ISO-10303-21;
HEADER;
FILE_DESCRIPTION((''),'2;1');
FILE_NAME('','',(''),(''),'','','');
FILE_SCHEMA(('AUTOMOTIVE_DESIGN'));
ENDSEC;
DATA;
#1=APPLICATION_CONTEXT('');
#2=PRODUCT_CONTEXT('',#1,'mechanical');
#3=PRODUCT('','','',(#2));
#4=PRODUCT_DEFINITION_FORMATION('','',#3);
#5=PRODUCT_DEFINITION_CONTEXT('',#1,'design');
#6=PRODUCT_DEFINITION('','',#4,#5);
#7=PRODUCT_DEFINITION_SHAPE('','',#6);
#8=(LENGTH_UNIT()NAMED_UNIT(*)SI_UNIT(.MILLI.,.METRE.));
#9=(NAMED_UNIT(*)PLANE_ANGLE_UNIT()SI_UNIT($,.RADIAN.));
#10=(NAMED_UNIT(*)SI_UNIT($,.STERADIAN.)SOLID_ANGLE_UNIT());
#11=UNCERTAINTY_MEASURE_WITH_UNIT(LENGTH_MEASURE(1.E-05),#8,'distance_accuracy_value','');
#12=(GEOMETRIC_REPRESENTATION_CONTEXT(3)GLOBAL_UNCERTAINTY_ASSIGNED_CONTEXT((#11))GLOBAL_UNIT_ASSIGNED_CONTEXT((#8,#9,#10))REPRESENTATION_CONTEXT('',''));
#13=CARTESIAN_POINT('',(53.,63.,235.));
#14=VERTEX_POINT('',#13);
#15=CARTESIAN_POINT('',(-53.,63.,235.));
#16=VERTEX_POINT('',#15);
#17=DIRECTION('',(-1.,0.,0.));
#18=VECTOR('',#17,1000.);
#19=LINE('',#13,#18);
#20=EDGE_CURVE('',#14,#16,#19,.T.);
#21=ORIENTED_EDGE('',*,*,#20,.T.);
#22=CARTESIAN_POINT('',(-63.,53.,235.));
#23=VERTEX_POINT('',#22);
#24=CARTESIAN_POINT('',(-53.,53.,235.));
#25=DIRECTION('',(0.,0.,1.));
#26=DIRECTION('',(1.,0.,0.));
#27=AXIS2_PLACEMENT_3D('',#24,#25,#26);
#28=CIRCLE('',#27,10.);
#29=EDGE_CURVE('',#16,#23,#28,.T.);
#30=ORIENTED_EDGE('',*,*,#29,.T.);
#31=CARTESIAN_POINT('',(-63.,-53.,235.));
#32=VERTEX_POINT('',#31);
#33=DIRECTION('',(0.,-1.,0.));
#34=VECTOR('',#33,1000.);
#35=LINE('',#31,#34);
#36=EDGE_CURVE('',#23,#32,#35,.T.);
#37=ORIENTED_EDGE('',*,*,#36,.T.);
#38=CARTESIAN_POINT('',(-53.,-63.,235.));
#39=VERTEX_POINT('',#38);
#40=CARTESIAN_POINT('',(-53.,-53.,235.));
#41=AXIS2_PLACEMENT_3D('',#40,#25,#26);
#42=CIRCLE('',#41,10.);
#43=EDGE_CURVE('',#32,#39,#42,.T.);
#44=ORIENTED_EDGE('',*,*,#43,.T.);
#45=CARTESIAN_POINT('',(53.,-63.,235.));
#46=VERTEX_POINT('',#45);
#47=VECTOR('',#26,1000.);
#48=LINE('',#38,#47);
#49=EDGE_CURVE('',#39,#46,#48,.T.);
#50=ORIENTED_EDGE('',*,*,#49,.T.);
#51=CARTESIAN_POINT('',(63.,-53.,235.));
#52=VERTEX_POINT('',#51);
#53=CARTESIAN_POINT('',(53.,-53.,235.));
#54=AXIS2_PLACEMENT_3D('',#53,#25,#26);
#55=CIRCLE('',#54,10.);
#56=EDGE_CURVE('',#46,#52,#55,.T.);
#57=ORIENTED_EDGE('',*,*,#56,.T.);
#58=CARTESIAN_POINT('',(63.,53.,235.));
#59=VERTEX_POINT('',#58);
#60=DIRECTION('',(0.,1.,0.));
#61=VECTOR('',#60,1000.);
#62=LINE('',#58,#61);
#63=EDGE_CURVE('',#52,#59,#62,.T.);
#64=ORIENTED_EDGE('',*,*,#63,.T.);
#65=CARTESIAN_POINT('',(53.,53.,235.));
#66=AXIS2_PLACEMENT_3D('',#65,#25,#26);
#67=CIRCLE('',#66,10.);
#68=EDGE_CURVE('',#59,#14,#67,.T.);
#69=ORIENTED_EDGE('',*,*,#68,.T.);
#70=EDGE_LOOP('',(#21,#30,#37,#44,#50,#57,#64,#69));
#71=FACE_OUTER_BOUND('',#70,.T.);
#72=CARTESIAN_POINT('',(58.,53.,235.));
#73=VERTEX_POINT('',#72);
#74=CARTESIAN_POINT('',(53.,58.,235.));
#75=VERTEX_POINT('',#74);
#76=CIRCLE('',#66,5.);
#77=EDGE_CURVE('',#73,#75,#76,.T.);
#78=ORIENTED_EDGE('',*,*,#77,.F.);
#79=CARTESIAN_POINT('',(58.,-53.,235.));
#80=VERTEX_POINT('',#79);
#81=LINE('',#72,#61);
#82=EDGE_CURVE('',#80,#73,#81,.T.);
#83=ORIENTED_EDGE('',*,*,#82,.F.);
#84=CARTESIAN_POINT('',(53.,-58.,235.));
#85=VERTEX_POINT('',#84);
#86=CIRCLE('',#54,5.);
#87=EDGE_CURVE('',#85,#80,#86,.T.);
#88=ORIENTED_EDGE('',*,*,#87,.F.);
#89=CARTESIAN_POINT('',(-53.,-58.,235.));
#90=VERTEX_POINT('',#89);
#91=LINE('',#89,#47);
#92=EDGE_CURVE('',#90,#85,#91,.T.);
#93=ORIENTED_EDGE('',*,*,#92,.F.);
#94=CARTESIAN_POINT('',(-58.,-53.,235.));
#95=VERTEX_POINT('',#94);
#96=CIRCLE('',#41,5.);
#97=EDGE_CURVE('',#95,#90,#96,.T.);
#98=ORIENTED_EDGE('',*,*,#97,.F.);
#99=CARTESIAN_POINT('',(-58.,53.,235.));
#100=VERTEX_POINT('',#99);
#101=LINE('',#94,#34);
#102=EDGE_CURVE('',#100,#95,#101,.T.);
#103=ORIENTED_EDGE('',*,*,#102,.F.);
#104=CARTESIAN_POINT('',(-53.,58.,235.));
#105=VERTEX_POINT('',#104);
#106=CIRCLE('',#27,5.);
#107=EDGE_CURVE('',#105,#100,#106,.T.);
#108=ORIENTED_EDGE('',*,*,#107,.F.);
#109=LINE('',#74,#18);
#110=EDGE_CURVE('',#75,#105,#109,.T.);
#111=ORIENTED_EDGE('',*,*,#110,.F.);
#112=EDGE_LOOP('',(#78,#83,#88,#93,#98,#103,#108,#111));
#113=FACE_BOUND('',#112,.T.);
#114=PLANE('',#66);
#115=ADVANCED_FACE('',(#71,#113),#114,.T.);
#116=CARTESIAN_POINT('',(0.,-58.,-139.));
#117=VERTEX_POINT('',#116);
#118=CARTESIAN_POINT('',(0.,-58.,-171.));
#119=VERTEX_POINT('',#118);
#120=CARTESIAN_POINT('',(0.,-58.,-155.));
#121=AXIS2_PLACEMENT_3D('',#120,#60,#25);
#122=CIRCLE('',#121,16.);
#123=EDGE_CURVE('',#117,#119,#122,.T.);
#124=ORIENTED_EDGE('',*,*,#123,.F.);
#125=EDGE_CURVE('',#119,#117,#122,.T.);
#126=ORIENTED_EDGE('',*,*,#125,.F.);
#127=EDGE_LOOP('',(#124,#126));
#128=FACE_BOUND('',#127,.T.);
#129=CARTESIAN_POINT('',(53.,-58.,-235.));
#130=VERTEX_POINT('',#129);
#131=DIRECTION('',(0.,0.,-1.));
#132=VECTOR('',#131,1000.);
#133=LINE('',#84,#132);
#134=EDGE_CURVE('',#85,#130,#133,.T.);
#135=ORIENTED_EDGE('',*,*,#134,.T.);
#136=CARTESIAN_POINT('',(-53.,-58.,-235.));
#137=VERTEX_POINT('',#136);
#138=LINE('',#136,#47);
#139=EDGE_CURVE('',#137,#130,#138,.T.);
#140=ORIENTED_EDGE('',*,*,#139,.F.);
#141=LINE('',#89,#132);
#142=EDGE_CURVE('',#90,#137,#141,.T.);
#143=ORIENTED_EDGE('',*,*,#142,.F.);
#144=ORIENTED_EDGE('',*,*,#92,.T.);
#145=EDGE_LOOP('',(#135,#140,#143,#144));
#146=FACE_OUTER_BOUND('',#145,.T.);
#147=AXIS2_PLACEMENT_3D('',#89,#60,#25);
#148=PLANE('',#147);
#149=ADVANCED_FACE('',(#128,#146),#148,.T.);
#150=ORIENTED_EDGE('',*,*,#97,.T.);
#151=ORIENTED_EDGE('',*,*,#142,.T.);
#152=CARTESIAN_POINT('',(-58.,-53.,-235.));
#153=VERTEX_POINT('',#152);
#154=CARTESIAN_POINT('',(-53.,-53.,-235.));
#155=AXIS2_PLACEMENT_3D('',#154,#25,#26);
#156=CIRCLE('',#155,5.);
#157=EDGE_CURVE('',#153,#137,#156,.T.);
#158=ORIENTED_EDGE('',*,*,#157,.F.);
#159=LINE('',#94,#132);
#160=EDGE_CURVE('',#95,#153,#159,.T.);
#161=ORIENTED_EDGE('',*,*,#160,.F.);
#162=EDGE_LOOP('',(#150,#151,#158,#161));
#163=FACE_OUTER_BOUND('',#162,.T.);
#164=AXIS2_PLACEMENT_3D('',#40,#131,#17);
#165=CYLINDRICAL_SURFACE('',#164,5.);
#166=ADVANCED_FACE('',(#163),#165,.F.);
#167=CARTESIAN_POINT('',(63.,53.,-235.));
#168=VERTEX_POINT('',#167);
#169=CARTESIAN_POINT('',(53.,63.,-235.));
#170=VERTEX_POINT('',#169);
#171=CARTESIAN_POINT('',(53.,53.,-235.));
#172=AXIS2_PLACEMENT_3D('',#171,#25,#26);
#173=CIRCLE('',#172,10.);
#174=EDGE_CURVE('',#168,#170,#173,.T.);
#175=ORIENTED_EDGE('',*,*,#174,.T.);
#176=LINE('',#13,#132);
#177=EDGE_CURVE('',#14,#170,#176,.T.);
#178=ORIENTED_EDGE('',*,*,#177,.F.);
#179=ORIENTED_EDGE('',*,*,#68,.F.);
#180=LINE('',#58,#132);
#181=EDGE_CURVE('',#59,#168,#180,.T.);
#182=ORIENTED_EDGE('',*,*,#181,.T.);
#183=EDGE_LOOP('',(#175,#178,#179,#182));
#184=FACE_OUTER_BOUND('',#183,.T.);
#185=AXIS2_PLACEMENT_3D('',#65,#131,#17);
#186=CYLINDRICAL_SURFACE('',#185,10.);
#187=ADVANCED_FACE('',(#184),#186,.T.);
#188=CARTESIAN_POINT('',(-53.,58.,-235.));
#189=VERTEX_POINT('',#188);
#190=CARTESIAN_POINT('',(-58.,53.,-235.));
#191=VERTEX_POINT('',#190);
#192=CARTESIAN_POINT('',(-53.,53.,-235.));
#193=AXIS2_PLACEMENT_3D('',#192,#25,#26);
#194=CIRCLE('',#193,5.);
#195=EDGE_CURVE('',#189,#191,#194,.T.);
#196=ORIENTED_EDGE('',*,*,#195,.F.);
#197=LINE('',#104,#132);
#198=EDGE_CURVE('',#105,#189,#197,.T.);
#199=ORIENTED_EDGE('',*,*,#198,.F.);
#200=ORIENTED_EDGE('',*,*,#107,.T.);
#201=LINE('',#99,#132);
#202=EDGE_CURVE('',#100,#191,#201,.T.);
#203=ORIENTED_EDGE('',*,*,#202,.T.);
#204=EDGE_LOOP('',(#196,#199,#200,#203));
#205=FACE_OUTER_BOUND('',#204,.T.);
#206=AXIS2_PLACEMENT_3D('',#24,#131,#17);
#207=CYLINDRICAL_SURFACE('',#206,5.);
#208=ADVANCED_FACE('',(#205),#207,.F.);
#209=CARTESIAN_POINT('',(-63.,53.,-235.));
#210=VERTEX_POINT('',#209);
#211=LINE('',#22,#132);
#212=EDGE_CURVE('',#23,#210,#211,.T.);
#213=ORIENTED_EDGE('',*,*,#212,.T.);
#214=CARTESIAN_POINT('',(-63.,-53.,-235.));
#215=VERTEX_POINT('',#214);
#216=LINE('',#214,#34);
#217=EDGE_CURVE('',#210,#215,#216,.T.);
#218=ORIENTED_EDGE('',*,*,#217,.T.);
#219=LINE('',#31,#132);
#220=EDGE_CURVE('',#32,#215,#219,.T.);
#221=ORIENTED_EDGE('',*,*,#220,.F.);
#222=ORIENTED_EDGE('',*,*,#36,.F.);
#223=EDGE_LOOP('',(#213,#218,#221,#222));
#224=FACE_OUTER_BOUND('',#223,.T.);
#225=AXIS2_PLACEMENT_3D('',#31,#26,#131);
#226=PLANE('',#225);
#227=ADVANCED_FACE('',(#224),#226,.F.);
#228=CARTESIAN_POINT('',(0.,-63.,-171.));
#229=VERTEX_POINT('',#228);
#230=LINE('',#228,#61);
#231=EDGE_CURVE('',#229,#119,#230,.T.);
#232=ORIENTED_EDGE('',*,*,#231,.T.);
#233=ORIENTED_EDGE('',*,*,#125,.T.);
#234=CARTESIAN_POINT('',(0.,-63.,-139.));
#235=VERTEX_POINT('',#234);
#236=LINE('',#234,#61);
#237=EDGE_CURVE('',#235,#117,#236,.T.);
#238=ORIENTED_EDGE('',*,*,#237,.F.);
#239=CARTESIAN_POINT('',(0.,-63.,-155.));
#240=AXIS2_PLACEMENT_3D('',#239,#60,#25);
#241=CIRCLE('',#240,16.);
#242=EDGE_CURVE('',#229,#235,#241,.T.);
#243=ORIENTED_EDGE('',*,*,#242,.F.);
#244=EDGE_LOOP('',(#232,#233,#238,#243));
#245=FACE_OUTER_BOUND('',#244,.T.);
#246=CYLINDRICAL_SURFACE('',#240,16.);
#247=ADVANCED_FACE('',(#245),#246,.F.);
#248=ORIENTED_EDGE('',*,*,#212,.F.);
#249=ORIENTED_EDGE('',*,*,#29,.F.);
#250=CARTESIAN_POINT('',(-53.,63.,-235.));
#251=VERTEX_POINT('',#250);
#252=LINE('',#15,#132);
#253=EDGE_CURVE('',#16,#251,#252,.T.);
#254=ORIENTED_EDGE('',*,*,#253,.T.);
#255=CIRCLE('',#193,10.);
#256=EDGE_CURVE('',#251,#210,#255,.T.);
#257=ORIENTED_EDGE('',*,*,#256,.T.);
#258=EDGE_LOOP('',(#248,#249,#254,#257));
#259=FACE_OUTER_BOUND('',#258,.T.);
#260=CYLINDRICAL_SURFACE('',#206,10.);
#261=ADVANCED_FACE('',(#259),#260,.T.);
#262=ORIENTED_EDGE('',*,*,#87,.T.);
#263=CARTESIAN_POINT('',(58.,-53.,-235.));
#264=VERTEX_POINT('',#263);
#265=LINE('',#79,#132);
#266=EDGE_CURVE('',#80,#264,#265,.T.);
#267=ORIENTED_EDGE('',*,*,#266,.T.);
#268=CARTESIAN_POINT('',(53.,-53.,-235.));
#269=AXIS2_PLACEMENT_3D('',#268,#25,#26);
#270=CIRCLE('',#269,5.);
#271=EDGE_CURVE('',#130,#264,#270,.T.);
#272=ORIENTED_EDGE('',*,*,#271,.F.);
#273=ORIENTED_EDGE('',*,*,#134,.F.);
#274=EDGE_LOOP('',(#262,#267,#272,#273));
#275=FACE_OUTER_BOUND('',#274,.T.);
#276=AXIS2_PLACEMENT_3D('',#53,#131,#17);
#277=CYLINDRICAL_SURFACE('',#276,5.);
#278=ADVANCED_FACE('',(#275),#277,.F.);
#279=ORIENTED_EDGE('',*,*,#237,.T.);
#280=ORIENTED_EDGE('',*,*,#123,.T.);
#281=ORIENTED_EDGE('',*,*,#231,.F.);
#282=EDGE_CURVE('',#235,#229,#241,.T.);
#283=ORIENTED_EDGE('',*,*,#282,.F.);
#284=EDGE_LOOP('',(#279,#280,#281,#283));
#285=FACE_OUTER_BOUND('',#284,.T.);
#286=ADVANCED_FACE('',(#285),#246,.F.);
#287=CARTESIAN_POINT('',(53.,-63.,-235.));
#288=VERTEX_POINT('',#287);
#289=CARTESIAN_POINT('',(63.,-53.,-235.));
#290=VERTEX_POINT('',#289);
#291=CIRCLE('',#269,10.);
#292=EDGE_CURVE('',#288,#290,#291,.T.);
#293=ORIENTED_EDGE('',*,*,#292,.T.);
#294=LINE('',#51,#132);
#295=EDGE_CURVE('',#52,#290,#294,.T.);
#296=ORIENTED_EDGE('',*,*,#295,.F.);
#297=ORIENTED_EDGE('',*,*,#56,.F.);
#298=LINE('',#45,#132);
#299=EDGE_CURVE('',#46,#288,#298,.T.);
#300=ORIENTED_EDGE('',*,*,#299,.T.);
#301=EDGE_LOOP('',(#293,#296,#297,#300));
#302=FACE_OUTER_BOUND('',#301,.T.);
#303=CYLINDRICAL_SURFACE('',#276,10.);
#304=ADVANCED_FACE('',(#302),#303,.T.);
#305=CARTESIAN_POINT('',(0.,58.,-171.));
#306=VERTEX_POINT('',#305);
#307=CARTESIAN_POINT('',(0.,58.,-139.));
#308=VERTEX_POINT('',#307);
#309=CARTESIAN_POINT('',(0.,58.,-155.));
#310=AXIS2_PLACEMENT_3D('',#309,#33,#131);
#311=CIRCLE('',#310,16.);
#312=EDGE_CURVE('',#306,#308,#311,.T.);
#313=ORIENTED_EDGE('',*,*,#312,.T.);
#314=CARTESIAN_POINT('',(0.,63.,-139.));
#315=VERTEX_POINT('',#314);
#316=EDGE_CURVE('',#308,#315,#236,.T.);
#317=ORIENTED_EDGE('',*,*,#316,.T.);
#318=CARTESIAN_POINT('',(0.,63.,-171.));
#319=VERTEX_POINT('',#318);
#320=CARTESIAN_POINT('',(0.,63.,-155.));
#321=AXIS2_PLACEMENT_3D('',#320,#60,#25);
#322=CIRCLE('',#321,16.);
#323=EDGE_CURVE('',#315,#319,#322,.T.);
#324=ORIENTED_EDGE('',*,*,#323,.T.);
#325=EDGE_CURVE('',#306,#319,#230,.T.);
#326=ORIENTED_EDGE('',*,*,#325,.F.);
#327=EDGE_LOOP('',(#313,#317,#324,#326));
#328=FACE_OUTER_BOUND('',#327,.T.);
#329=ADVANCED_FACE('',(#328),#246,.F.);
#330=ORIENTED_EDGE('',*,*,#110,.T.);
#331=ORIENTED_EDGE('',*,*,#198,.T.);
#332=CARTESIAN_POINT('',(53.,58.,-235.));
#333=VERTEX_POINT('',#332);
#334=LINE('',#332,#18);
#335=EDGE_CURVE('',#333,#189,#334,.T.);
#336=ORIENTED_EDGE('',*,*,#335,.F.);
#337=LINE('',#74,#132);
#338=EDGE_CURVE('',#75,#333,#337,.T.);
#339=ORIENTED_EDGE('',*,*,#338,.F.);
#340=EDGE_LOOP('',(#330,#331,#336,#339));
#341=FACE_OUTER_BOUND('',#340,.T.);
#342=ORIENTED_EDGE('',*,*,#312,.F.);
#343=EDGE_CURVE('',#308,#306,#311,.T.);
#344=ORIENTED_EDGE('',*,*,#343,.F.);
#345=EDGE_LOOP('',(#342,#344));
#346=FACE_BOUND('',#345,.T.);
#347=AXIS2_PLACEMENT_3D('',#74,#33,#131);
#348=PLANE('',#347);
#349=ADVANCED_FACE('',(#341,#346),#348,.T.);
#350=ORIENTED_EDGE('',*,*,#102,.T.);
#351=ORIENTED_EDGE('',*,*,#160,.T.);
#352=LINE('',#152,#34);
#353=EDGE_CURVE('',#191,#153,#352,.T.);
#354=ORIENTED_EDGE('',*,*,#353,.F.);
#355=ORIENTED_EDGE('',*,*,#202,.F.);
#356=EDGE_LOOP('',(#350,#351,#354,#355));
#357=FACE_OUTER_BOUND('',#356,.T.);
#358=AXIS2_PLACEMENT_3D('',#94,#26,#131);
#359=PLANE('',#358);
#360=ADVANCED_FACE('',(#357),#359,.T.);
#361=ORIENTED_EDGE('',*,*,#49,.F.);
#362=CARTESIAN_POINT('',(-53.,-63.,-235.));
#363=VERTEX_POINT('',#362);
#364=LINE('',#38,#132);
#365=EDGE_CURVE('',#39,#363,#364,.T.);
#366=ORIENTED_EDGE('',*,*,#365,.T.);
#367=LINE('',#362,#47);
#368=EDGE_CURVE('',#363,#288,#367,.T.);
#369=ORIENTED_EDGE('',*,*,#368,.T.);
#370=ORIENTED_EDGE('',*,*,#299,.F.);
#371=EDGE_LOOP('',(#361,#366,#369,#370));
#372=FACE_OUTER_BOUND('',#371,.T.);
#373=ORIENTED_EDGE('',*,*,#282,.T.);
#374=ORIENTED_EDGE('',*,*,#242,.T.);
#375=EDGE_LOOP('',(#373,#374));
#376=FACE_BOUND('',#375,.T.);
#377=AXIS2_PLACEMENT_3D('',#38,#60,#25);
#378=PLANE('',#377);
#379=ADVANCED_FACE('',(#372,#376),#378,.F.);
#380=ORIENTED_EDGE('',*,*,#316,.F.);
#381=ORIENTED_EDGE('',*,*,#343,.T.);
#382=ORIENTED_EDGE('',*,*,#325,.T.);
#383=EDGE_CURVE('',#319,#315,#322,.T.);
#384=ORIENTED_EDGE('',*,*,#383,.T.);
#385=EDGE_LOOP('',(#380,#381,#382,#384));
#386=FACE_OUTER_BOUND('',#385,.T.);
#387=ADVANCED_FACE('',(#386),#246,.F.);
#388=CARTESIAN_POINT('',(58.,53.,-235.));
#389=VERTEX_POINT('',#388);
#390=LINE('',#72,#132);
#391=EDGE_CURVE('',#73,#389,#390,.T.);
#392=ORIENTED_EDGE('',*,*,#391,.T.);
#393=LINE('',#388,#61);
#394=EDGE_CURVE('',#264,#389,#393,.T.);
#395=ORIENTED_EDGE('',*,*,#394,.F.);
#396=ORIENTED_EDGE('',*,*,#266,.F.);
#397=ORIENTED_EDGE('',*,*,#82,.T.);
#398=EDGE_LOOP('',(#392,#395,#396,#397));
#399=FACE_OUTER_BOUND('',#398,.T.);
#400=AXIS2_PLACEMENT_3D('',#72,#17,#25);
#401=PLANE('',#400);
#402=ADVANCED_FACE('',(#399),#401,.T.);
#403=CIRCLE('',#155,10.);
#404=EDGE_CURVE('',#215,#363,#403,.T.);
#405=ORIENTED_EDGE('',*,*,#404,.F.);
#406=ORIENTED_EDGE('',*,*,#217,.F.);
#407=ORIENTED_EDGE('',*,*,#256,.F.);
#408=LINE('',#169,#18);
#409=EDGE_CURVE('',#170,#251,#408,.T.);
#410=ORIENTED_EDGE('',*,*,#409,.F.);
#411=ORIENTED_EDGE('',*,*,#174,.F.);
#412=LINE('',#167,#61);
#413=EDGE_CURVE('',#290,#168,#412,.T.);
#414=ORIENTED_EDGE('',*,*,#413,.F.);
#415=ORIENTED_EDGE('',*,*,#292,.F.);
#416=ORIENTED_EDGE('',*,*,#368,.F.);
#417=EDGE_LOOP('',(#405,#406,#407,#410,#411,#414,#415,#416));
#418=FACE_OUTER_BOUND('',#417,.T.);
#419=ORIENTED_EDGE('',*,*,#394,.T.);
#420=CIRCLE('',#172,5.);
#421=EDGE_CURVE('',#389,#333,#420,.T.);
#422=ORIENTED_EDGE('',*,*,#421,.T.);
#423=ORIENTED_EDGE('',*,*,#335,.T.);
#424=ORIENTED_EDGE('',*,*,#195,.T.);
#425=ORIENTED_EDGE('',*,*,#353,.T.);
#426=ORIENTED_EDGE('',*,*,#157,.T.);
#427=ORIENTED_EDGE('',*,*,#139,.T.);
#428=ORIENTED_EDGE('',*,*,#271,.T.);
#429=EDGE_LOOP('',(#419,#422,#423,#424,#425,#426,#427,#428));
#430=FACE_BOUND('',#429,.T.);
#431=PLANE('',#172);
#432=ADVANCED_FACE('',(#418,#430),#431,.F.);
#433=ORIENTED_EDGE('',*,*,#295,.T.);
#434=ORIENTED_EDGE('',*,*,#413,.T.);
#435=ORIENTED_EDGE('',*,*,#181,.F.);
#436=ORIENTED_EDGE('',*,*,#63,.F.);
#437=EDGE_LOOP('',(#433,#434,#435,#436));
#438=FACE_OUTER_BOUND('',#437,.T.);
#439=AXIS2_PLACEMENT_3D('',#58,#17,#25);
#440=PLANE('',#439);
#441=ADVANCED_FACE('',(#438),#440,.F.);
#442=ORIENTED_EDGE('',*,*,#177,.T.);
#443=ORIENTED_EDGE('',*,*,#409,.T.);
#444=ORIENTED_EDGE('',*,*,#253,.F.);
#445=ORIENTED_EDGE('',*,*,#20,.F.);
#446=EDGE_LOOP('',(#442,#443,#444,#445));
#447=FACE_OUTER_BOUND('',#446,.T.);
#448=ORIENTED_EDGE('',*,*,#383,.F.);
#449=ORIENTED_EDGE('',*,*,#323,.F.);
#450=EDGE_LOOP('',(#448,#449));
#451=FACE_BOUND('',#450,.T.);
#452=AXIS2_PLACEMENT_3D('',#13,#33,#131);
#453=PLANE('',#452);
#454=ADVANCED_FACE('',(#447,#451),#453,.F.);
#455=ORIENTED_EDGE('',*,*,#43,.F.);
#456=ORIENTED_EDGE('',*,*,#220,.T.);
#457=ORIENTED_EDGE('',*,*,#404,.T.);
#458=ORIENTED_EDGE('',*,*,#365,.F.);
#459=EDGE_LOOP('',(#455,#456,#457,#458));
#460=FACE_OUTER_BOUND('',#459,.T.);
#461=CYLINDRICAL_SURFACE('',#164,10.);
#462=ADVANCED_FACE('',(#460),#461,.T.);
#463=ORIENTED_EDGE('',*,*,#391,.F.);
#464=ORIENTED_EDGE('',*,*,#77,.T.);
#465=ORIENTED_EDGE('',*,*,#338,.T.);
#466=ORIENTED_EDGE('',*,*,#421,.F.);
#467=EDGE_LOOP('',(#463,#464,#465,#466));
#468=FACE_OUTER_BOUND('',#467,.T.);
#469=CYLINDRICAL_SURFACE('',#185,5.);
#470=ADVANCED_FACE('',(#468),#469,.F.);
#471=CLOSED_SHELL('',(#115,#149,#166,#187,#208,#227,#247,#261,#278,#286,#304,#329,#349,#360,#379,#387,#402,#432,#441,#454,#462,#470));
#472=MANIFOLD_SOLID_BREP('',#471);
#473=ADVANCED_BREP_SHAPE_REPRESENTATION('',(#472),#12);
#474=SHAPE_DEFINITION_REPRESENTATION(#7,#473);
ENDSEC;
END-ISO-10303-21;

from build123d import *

# Parameters (mm, degrees)
BOSS_EXTRUDE1_DEPTH     = 235
CUT_EXTRUDE1_DEPTH      = 252.322501977
CUT_EXTRUDE1_DEPTH_BACK = 252.322501977
SKETCH_1_R              = 16


with BuildPart() as part:
    # Sketch1 → Boss-Extrude1 (new, symmetric)
    with BuildSketch(Plane.XY):
        with BuildLine():
            Line((-53, -63), (53, -63))
            ThreePointArc((53, -63), (60.071067812, -60.071067812), (63, -53))
            Line((63, -53), (63, 53))
            ThreePointArc((63, 53), (60.071067812, 60.071067812), (53, 63))
            Line((53, 63), (-53, 63))
            ThreePointArc((-53, 63), (-60.071067812, 60.071067812), (-63, 53))
            Line((-63, 53), (-63, -53))
            ThreePointArc((-63, -53), (-60.071067812, -60.071067812), (-53, -63))
        make_face()
        with BuildLine():
            Line((-53, -58), (53, -58))
            ThreePointArc((53, -58), (56.535533906, -56.535533906), (58, -53))
            Line((58, -53), (58, 53))
            ThreePointArc((58, 53), (56.535533906, 56.535533906), (53, 58))
            Line((53, 58), (-53, 58))
            ThreePointArc((-53, 58), (-56.535533906, 56.535533906), (-58, 53))
            Line((-58, 53), (-58, -53))
            ThreePointArc((-58, -53), (-56.535533906, -56.535533906), (-53, -58))
        make_face(mode=Mode.SUBTRACT)
    extrude(amount=BOSS_EXTRUDE1_DEPTH, both=True)

    # 草图1 → Cut-Extrude1 (cut, two sides: drawn at the far end of the back side and taken through both)
    with BuildSketch(Plane(origin=(0, 0, 0), x_dir=(1, 0, 0), z_dir=(0, 1, 0)).offset(-CUT_EXTRUDE1_DEPTH_BACK)):
        with Locations(Location((0, 155, 0), (0, 0, 270))):
            Circle(SKETCH_1_R)
    extrude(amount=CUT_EXTRUDE1_DEPTH + CUT_EXTRUDE1_DEPTH_BACK, mode=Mode.SUBTRACT)


solid = part.part
